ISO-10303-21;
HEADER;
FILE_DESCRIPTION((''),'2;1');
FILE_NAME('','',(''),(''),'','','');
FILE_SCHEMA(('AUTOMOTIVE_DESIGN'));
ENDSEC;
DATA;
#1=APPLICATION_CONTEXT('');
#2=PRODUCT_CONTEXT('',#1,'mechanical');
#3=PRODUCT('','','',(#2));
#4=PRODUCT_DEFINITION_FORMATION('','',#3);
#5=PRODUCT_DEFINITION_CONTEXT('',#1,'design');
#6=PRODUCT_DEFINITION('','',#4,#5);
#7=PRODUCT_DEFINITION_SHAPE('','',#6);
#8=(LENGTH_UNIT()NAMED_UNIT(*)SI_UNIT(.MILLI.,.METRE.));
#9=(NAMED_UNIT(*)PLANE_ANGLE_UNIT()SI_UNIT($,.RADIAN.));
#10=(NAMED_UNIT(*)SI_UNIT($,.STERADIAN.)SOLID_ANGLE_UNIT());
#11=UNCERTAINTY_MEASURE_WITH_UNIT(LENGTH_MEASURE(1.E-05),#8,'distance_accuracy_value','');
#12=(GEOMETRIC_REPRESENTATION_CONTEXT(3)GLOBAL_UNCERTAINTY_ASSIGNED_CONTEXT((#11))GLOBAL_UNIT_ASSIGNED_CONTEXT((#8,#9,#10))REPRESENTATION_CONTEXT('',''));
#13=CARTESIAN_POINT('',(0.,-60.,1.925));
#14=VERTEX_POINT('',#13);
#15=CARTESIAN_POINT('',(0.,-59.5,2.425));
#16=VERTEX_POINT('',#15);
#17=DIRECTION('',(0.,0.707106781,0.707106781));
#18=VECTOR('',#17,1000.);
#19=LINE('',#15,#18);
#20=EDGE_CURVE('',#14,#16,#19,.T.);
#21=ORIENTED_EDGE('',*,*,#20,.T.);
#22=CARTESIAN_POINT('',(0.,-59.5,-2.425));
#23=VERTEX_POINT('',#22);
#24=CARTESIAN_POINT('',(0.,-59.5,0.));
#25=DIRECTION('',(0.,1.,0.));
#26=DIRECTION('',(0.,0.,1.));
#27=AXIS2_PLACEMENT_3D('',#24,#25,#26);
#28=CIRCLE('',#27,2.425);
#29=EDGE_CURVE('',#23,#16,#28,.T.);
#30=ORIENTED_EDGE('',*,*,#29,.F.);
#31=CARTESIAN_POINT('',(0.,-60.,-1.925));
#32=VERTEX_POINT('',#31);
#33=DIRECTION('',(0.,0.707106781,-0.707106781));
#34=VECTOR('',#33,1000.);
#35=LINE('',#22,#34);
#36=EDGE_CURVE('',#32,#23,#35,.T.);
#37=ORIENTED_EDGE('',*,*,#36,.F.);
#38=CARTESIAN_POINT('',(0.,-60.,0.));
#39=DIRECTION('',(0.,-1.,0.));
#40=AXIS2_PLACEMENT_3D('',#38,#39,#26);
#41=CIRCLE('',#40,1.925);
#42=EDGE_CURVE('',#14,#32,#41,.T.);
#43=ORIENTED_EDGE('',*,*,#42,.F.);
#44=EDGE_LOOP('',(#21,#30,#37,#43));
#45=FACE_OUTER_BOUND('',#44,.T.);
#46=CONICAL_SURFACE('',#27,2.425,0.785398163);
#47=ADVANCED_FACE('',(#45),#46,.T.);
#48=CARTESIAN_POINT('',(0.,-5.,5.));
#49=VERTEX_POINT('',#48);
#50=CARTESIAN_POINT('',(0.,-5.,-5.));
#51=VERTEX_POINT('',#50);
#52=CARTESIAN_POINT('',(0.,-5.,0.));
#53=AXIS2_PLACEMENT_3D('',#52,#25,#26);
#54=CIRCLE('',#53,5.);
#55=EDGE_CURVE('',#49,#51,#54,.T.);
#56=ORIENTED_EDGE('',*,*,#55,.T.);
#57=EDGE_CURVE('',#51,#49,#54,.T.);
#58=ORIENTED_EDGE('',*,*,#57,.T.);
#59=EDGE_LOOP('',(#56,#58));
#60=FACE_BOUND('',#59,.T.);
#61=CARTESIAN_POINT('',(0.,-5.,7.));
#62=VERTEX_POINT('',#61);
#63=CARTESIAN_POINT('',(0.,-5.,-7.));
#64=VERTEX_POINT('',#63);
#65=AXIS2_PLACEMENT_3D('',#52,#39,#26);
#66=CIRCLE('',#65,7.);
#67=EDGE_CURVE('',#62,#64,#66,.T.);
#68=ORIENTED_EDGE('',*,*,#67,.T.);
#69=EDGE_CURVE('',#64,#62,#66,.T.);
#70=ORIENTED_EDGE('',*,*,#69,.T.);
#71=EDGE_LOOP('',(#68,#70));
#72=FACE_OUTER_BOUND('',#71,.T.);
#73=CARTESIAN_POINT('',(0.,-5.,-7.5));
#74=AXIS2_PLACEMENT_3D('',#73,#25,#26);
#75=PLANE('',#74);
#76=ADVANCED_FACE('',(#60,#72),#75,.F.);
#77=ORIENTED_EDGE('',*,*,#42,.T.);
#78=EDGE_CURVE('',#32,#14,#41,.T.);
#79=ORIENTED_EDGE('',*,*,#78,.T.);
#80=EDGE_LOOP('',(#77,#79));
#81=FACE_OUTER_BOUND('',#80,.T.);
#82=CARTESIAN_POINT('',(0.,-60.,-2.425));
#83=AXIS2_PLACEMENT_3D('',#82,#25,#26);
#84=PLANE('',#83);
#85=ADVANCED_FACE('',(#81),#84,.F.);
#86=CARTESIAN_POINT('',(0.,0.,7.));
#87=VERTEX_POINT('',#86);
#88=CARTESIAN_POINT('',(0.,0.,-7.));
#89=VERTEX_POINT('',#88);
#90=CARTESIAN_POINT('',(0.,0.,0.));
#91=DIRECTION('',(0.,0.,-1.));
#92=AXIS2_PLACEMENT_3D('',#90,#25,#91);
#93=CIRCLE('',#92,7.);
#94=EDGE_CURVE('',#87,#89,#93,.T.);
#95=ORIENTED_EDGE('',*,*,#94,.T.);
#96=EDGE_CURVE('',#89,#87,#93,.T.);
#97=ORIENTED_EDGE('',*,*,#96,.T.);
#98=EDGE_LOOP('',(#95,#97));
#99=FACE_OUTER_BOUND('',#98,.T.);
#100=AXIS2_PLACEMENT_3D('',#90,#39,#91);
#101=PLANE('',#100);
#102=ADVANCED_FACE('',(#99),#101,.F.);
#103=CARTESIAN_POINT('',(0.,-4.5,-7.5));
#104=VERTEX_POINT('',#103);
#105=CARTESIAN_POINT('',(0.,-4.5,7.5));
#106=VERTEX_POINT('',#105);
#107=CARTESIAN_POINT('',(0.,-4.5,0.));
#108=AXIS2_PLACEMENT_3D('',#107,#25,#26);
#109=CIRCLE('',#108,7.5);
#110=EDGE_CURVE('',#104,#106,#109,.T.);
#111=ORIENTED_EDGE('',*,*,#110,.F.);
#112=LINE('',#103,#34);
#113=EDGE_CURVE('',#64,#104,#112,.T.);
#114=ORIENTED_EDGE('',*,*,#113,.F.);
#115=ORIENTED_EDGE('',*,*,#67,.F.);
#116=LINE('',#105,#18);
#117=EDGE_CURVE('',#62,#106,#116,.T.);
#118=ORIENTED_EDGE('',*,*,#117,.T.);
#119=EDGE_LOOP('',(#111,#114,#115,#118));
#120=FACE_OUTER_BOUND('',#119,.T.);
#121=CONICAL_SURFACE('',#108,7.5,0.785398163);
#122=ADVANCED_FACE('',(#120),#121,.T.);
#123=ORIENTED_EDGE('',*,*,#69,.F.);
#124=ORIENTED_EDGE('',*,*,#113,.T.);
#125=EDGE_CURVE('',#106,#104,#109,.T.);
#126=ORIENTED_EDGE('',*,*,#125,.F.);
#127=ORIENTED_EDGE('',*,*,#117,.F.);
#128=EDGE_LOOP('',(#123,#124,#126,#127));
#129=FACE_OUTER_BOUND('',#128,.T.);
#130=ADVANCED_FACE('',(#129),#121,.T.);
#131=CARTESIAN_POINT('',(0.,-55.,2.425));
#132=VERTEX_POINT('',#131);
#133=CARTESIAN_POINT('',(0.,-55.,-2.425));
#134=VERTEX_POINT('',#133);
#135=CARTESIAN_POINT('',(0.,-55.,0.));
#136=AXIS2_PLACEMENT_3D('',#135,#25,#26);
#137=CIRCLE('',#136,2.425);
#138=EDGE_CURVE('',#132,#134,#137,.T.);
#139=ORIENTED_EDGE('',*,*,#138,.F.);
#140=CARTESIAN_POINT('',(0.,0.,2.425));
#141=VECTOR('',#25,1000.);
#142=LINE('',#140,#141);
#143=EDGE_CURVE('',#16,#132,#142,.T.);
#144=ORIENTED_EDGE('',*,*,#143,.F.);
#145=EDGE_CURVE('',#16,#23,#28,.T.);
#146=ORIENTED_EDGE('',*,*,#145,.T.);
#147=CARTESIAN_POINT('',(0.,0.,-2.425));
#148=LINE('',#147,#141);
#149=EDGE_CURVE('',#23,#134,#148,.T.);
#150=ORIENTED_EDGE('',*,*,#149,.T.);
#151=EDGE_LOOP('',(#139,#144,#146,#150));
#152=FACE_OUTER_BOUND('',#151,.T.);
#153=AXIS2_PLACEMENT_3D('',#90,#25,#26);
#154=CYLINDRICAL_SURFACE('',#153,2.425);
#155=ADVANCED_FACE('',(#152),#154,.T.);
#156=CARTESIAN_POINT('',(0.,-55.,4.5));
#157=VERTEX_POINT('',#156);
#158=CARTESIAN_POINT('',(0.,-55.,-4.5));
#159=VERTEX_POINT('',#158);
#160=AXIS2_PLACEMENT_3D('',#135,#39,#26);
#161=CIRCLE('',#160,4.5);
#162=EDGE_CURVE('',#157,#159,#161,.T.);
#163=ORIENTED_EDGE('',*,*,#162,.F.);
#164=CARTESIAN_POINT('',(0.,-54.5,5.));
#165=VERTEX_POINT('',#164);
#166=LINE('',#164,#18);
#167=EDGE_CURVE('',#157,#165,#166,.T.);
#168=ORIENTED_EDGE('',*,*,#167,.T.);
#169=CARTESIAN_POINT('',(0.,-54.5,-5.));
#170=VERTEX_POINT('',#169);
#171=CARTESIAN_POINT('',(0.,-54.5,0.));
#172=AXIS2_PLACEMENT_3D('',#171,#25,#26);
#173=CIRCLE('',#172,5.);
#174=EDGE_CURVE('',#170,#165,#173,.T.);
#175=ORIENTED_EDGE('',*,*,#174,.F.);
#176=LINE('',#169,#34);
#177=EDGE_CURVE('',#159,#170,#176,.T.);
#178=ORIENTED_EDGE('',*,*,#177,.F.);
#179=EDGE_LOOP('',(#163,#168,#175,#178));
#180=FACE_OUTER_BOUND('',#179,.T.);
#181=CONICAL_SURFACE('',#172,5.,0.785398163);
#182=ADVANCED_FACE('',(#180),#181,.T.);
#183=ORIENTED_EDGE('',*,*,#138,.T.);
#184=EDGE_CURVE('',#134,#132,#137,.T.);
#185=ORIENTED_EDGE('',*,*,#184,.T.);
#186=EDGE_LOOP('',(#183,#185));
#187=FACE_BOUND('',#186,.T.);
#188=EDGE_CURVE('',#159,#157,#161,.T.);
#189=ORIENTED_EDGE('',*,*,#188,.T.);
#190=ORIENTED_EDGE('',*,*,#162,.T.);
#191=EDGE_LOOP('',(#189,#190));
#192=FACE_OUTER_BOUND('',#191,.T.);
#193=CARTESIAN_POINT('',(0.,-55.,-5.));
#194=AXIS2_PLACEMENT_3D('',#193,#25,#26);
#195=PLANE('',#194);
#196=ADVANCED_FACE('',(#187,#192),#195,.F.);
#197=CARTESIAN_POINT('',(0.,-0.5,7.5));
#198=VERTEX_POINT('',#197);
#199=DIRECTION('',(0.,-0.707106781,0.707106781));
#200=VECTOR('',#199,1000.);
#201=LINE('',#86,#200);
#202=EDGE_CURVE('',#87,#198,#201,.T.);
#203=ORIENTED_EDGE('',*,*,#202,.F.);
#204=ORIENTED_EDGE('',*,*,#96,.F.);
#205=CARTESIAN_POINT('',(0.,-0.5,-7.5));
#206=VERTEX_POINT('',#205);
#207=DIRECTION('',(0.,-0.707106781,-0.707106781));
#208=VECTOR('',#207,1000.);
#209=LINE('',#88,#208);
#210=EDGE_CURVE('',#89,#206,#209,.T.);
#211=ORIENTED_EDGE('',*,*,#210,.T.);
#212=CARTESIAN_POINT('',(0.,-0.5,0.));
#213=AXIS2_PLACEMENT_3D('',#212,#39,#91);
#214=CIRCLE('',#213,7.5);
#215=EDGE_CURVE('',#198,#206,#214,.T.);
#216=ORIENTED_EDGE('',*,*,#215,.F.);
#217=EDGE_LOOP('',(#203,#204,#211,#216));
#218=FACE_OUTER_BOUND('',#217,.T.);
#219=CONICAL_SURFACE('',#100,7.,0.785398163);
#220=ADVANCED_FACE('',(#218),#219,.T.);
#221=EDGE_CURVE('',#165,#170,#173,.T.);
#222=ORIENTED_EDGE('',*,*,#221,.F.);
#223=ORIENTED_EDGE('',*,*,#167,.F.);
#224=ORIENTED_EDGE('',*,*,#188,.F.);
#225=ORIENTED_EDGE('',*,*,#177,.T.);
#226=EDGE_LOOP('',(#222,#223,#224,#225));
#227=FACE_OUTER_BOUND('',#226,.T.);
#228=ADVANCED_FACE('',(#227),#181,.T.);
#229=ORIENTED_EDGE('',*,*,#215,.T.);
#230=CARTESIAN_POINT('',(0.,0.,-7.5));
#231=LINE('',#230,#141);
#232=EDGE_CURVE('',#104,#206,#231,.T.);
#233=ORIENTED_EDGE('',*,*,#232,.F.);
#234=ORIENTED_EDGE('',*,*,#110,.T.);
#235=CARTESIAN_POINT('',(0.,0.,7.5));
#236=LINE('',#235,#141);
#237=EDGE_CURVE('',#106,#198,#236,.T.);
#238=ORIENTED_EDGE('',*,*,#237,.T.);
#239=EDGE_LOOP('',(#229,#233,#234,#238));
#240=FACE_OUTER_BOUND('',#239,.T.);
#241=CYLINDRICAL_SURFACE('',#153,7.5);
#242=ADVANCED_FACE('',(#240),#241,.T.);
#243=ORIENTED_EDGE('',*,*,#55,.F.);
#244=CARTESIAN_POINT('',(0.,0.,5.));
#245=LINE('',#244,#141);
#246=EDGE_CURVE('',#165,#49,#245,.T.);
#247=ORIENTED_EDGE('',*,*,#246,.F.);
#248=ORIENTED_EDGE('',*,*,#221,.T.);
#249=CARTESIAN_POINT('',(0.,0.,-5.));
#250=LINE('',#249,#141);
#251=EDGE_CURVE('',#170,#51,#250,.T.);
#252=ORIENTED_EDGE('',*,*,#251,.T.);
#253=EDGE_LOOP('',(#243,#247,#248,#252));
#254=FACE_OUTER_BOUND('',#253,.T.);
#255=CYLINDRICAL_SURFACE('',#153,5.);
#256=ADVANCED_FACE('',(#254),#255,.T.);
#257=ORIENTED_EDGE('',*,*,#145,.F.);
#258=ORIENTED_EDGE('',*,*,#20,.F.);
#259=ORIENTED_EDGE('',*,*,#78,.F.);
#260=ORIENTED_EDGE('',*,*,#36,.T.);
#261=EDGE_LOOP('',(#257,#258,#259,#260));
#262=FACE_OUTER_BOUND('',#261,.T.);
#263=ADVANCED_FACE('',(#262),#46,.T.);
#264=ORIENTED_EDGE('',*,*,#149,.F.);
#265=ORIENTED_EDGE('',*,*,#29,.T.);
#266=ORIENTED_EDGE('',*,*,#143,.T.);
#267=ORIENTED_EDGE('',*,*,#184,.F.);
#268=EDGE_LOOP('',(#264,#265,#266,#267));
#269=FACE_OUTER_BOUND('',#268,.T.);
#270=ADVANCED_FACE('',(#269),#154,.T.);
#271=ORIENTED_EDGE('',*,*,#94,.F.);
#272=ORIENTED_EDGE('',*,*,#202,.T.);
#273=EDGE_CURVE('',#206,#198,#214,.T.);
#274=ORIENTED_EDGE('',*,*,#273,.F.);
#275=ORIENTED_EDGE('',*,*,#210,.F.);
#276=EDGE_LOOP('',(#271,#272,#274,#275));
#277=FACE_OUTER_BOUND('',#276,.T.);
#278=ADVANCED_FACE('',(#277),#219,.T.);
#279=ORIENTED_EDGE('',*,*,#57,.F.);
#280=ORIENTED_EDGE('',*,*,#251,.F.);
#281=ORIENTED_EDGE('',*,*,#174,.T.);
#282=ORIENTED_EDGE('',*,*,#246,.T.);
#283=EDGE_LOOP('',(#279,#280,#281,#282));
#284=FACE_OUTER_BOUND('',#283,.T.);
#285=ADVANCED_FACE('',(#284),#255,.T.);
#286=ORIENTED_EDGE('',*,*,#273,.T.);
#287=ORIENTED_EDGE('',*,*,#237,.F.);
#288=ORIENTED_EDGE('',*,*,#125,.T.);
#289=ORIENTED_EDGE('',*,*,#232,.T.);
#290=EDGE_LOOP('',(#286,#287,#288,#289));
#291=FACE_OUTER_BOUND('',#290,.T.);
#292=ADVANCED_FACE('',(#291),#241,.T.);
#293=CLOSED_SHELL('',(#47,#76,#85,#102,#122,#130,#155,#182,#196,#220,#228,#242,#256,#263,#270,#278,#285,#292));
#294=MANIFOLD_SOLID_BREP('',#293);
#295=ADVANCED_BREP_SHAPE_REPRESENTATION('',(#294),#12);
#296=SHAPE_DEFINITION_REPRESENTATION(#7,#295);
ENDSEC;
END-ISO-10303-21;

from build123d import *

# Parameters (mm, degrees)
CHAMFER1_SIZE = 0.5


with BuildPart() as part:
    # Sketch1 → Revolve1 (revolve)
    with BuildSketch(Plane(origin=(0, 0, 0), x_dir=(0, 0, -1), z_dir=(1, 0, 0)), mode=Mode.PRIVATE) as revolve1_sk:
        Polygon((0, 0), (7.5, 0), (7.5, -5), (5, -5), (5, -55), (2.425, -55), (2.425, -60), (0, -60), align=None)
    revolve(revolve1_sk.sketch.rotate(Axis((0, 0, 0), (0, -1, 0)), 180), axis=Axis((0, 0, 0), (0, -1, 0)))

    # Chamfer1
    chamfer1_edges = [part.edges().sort_by_distance(p)[0] for p in [
        (0, -60, -2.425),
        (0, -55, -5),
        (0, -5, -7.5),
        (0, 0, -7.5),
    ]]
    chamfer(chamfer1_edges, length=CHAMFER1_SIZE)


solid = part.part
